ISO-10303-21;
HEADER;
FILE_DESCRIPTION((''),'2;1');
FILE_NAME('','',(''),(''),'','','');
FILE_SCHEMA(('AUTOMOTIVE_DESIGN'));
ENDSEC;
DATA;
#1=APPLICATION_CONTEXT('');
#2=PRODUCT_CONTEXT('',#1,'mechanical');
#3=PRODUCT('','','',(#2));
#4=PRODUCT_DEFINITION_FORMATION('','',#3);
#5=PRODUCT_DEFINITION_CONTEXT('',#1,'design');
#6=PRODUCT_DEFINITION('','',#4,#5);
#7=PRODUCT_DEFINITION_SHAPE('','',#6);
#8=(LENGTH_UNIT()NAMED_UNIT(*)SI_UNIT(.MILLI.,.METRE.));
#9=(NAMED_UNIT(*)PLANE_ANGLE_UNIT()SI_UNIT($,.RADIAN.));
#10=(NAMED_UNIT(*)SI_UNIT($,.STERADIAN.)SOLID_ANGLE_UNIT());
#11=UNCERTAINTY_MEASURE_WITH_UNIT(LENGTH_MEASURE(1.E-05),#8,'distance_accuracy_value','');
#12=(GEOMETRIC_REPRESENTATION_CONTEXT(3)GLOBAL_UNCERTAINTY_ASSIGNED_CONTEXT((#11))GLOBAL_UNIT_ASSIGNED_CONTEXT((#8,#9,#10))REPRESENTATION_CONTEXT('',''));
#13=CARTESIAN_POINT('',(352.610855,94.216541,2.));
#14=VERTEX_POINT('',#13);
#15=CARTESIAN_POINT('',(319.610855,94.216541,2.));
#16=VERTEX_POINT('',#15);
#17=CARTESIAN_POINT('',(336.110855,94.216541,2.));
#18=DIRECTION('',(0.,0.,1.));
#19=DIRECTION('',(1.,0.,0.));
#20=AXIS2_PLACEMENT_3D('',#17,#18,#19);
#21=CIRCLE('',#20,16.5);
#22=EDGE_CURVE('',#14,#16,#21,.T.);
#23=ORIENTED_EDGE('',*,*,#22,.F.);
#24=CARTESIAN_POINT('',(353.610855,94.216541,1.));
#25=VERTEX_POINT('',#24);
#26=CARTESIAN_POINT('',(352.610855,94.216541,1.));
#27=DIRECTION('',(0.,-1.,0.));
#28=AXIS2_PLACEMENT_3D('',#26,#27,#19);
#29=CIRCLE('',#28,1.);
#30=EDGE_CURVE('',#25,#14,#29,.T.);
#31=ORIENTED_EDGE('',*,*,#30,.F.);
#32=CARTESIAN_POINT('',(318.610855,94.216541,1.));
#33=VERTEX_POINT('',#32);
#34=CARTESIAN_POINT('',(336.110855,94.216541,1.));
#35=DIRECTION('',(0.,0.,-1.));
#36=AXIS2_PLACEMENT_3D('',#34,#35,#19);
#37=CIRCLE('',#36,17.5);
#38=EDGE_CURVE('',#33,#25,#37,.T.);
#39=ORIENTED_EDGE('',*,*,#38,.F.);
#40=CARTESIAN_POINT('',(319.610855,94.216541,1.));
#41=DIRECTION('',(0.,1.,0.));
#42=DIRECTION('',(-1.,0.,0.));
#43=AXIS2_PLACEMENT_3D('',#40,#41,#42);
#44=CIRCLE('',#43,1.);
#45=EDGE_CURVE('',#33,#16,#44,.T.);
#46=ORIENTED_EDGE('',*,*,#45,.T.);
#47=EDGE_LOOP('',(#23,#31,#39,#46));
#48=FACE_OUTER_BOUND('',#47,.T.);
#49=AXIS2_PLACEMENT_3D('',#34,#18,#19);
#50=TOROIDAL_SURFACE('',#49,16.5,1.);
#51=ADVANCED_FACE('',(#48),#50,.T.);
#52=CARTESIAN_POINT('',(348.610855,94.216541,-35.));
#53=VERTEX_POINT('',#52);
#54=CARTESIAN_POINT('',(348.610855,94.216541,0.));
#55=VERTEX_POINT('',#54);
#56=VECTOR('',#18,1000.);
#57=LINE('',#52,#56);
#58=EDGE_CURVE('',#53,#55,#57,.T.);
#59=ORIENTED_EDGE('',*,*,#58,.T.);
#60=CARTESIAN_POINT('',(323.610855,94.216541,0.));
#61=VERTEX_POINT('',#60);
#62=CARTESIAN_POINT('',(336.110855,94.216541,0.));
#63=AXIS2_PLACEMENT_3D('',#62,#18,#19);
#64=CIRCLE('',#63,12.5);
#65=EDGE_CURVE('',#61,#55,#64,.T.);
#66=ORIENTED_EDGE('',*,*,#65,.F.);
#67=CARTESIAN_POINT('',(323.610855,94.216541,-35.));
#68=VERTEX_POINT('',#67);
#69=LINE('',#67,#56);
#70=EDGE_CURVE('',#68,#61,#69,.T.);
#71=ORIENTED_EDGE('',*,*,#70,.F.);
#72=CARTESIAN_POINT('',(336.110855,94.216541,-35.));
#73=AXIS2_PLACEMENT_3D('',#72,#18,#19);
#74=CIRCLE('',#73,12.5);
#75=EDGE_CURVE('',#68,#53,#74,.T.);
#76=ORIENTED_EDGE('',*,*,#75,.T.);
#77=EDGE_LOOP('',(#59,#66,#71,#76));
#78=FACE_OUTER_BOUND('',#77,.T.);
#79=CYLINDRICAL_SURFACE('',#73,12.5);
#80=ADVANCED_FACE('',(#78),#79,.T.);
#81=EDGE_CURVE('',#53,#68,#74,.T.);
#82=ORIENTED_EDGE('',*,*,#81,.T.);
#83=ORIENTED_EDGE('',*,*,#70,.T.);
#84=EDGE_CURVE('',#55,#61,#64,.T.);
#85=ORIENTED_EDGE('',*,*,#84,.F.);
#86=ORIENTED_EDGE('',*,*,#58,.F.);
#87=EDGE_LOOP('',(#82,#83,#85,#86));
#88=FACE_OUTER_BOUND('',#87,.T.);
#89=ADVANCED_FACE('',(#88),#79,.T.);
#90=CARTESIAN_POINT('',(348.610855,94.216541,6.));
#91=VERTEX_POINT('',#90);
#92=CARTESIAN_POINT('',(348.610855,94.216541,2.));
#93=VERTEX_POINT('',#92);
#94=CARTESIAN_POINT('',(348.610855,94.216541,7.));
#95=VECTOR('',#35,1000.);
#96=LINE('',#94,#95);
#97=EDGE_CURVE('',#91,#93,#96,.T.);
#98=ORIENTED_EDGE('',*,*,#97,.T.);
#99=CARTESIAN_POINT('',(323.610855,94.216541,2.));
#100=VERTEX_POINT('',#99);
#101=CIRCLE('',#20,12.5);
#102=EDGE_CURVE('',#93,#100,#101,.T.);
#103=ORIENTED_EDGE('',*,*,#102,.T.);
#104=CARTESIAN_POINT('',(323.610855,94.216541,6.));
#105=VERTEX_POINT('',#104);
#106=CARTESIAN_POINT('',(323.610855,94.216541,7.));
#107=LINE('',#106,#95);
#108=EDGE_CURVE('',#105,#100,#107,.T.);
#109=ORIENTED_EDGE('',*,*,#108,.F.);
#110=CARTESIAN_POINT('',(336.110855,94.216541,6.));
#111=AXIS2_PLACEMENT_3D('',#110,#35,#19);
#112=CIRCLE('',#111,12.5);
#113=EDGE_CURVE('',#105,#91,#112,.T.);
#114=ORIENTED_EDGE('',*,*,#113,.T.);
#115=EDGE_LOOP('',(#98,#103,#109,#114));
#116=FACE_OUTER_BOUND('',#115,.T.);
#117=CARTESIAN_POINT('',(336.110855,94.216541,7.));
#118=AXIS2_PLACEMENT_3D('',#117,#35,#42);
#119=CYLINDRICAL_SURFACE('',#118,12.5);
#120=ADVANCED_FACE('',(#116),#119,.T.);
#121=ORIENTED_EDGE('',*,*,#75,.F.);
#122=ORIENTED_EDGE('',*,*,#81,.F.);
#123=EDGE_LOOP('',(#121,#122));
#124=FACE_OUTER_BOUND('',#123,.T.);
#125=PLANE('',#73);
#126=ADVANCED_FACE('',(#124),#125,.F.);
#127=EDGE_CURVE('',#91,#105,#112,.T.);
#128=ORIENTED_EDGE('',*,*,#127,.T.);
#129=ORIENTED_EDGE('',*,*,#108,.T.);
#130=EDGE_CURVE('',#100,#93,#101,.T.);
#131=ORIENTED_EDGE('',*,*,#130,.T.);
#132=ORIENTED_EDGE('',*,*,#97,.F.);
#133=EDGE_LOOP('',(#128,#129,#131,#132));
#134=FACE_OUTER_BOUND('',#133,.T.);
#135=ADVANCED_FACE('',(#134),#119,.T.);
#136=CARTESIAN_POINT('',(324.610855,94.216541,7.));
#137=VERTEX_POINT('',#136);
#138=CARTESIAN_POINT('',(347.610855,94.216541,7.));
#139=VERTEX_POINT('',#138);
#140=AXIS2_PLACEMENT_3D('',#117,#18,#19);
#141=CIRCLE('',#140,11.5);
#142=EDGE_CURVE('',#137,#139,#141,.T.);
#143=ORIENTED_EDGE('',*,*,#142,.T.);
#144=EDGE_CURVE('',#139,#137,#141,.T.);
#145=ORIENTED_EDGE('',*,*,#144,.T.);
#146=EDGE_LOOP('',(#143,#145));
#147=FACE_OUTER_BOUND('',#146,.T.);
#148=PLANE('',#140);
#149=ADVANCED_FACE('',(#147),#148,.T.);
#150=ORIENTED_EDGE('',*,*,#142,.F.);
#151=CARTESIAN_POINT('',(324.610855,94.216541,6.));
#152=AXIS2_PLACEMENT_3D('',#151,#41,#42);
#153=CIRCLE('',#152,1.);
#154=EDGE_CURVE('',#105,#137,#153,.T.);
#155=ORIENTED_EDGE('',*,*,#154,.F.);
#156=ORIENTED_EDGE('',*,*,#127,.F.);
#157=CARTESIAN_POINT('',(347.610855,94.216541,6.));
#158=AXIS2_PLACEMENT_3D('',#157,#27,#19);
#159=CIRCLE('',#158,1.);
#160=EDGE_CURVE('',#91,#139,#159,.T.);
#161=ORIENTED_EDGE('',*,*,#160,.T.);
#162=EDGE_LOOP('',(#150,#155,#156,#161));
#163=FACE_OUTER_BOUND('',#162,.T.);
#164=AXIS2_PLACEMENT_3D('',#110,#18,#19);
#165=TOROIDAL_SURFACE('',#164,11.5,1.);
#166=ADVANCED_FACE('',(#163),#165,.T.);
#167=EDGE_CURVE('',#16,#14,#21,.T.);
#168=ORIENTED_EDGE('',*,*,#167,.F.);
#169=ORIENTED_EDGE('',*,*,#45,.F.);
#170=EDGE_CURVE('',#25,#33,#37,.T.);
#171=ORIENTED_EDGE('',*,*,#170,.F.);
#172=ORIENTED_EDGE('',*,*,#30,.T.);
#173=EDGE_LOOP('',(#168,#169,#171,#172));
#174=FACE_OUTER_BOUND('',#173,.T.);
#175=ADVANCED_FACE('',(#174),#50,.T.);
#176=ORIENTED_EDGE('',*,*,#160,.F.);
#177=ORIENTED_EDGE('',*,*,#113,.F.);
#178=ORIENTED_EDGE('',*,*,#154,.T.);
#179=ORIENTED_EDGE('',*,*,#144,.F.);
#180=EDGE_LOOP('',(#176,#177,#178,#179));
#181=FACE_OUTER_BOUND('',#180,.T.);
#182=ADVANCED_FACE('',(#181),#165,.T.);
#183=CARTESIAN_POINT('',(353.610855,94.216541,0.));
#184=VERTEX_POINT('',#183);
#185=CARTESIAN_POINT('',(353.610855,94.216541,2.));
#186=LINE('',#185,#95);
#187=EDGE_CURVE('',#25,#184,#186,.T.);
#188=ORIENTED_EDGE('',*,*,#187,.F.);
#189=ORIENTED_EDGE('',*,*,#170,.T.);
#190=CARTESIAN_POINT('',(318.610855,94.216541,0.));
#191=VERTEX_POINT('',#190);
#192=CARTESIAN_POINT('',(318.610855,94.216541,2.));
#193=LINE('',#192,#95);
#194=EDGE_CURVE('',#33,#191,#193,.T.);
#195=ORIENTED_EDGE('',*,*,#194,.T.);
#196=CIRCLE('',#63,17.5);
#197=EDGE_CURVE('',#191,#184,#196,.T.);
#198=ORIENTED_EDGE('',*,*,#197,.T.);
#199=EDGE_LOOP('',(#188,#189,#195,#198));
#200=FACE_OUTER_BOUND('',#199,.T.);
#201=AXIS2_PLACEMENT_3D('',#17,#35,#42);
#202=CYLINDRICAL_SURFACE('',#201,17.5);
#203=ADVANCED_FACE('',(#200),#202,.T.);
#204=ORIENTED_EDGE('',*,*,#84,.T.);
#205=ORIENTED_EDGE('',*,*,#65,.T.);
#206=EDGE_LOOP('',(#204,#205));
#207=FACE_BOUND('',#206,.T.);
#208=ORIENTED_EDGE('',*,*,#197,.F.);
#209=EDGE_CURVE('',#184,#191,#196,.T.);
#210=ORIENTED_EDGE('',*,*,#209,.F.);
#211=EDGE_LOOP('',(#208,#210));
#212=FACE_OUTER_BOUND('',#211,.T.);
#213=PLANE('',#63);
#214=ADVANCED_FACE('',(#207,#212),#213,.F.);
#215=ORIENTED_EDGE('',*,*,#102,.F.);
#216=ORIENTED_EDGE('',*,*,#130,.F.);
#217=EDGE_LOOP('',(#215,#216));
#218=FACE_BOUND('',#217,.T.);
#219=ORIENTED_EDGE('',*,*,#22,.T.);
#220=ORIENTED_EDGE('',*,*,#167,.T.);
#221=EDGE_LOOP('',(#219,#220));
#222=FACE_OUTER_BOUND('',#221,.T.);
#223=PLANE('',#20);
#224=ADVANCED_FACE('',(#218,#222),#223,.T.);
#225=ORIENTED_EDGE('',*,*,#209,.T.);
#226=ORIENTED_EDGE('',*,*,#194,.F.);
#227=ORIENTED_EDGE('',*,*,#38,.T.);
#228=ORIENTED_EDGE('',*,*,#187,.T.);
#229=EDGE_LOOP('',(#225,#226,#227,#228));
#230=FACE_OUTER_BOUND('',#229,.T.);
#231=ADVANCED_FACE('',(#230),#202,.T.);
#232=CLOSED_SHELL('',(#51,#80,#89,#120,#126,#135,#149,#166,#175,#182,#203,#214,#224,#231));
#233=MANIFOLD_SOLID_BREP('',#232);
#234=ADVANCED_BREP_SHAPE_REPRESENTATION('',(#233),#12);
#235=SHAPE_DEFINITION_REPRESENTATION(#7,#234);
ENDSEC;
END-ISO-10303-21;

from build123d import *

# Parameters (mm, degrees)
SKETCH1_R           = 12.5
BOSS_EXTRUDE1_DEPTH = 35
SKETCH2_R           = 17.5
BOSS_EXTRUDE2_DEPTH = 2
BOSS_EXTRUDE3_START = 5
SKETCH3_R           = 12.5
BOSS_EXTRUDE3_DEPTH = 5
FILLET1_R           = 1


with BuildPart() as part:
    # Sketch1 → Boss-Extrude1 (new body)
    with BuildSketch(Plane.XY):
        with Locations((336.110854844, 94.216541461)):
            Circle(SKETCH1_R)
    extrude(amount=-BOSS_EXTRUDE1_DEPTH)

    # Sketch2 → Boss-Extrude2 (add)
    with BuildSketch(Plane.XY):
        with Locations((336.110854844, 94.216541461)):
            Circle(SKETCH2_R)
    extrude(amount=BOSS_EXTRUDE2_DEPTH)

    # Sketch3 → Boss-Extrude3 (add)
    with BuildSketch(Plane.XY.offset(2).offset(BOSS_EXTRUDE3_START)):
        with Locations((336.110854844, 94.216541461)):
            Circle(SKETCH3_R)
    extrude(amount=-BOSS_EXTRUDE3_DEPTH)

    # Fillet1
    fillet1_edges = [part.edges().sort_by_distance(p)[0] for p in [
        (323.610854844, 94.216541461, 7),
        (318.610854844, 94.216541461, 2),
    ]]
    fillet(fillet1_edges, radius=FILLET1_R)


solid = part.part
